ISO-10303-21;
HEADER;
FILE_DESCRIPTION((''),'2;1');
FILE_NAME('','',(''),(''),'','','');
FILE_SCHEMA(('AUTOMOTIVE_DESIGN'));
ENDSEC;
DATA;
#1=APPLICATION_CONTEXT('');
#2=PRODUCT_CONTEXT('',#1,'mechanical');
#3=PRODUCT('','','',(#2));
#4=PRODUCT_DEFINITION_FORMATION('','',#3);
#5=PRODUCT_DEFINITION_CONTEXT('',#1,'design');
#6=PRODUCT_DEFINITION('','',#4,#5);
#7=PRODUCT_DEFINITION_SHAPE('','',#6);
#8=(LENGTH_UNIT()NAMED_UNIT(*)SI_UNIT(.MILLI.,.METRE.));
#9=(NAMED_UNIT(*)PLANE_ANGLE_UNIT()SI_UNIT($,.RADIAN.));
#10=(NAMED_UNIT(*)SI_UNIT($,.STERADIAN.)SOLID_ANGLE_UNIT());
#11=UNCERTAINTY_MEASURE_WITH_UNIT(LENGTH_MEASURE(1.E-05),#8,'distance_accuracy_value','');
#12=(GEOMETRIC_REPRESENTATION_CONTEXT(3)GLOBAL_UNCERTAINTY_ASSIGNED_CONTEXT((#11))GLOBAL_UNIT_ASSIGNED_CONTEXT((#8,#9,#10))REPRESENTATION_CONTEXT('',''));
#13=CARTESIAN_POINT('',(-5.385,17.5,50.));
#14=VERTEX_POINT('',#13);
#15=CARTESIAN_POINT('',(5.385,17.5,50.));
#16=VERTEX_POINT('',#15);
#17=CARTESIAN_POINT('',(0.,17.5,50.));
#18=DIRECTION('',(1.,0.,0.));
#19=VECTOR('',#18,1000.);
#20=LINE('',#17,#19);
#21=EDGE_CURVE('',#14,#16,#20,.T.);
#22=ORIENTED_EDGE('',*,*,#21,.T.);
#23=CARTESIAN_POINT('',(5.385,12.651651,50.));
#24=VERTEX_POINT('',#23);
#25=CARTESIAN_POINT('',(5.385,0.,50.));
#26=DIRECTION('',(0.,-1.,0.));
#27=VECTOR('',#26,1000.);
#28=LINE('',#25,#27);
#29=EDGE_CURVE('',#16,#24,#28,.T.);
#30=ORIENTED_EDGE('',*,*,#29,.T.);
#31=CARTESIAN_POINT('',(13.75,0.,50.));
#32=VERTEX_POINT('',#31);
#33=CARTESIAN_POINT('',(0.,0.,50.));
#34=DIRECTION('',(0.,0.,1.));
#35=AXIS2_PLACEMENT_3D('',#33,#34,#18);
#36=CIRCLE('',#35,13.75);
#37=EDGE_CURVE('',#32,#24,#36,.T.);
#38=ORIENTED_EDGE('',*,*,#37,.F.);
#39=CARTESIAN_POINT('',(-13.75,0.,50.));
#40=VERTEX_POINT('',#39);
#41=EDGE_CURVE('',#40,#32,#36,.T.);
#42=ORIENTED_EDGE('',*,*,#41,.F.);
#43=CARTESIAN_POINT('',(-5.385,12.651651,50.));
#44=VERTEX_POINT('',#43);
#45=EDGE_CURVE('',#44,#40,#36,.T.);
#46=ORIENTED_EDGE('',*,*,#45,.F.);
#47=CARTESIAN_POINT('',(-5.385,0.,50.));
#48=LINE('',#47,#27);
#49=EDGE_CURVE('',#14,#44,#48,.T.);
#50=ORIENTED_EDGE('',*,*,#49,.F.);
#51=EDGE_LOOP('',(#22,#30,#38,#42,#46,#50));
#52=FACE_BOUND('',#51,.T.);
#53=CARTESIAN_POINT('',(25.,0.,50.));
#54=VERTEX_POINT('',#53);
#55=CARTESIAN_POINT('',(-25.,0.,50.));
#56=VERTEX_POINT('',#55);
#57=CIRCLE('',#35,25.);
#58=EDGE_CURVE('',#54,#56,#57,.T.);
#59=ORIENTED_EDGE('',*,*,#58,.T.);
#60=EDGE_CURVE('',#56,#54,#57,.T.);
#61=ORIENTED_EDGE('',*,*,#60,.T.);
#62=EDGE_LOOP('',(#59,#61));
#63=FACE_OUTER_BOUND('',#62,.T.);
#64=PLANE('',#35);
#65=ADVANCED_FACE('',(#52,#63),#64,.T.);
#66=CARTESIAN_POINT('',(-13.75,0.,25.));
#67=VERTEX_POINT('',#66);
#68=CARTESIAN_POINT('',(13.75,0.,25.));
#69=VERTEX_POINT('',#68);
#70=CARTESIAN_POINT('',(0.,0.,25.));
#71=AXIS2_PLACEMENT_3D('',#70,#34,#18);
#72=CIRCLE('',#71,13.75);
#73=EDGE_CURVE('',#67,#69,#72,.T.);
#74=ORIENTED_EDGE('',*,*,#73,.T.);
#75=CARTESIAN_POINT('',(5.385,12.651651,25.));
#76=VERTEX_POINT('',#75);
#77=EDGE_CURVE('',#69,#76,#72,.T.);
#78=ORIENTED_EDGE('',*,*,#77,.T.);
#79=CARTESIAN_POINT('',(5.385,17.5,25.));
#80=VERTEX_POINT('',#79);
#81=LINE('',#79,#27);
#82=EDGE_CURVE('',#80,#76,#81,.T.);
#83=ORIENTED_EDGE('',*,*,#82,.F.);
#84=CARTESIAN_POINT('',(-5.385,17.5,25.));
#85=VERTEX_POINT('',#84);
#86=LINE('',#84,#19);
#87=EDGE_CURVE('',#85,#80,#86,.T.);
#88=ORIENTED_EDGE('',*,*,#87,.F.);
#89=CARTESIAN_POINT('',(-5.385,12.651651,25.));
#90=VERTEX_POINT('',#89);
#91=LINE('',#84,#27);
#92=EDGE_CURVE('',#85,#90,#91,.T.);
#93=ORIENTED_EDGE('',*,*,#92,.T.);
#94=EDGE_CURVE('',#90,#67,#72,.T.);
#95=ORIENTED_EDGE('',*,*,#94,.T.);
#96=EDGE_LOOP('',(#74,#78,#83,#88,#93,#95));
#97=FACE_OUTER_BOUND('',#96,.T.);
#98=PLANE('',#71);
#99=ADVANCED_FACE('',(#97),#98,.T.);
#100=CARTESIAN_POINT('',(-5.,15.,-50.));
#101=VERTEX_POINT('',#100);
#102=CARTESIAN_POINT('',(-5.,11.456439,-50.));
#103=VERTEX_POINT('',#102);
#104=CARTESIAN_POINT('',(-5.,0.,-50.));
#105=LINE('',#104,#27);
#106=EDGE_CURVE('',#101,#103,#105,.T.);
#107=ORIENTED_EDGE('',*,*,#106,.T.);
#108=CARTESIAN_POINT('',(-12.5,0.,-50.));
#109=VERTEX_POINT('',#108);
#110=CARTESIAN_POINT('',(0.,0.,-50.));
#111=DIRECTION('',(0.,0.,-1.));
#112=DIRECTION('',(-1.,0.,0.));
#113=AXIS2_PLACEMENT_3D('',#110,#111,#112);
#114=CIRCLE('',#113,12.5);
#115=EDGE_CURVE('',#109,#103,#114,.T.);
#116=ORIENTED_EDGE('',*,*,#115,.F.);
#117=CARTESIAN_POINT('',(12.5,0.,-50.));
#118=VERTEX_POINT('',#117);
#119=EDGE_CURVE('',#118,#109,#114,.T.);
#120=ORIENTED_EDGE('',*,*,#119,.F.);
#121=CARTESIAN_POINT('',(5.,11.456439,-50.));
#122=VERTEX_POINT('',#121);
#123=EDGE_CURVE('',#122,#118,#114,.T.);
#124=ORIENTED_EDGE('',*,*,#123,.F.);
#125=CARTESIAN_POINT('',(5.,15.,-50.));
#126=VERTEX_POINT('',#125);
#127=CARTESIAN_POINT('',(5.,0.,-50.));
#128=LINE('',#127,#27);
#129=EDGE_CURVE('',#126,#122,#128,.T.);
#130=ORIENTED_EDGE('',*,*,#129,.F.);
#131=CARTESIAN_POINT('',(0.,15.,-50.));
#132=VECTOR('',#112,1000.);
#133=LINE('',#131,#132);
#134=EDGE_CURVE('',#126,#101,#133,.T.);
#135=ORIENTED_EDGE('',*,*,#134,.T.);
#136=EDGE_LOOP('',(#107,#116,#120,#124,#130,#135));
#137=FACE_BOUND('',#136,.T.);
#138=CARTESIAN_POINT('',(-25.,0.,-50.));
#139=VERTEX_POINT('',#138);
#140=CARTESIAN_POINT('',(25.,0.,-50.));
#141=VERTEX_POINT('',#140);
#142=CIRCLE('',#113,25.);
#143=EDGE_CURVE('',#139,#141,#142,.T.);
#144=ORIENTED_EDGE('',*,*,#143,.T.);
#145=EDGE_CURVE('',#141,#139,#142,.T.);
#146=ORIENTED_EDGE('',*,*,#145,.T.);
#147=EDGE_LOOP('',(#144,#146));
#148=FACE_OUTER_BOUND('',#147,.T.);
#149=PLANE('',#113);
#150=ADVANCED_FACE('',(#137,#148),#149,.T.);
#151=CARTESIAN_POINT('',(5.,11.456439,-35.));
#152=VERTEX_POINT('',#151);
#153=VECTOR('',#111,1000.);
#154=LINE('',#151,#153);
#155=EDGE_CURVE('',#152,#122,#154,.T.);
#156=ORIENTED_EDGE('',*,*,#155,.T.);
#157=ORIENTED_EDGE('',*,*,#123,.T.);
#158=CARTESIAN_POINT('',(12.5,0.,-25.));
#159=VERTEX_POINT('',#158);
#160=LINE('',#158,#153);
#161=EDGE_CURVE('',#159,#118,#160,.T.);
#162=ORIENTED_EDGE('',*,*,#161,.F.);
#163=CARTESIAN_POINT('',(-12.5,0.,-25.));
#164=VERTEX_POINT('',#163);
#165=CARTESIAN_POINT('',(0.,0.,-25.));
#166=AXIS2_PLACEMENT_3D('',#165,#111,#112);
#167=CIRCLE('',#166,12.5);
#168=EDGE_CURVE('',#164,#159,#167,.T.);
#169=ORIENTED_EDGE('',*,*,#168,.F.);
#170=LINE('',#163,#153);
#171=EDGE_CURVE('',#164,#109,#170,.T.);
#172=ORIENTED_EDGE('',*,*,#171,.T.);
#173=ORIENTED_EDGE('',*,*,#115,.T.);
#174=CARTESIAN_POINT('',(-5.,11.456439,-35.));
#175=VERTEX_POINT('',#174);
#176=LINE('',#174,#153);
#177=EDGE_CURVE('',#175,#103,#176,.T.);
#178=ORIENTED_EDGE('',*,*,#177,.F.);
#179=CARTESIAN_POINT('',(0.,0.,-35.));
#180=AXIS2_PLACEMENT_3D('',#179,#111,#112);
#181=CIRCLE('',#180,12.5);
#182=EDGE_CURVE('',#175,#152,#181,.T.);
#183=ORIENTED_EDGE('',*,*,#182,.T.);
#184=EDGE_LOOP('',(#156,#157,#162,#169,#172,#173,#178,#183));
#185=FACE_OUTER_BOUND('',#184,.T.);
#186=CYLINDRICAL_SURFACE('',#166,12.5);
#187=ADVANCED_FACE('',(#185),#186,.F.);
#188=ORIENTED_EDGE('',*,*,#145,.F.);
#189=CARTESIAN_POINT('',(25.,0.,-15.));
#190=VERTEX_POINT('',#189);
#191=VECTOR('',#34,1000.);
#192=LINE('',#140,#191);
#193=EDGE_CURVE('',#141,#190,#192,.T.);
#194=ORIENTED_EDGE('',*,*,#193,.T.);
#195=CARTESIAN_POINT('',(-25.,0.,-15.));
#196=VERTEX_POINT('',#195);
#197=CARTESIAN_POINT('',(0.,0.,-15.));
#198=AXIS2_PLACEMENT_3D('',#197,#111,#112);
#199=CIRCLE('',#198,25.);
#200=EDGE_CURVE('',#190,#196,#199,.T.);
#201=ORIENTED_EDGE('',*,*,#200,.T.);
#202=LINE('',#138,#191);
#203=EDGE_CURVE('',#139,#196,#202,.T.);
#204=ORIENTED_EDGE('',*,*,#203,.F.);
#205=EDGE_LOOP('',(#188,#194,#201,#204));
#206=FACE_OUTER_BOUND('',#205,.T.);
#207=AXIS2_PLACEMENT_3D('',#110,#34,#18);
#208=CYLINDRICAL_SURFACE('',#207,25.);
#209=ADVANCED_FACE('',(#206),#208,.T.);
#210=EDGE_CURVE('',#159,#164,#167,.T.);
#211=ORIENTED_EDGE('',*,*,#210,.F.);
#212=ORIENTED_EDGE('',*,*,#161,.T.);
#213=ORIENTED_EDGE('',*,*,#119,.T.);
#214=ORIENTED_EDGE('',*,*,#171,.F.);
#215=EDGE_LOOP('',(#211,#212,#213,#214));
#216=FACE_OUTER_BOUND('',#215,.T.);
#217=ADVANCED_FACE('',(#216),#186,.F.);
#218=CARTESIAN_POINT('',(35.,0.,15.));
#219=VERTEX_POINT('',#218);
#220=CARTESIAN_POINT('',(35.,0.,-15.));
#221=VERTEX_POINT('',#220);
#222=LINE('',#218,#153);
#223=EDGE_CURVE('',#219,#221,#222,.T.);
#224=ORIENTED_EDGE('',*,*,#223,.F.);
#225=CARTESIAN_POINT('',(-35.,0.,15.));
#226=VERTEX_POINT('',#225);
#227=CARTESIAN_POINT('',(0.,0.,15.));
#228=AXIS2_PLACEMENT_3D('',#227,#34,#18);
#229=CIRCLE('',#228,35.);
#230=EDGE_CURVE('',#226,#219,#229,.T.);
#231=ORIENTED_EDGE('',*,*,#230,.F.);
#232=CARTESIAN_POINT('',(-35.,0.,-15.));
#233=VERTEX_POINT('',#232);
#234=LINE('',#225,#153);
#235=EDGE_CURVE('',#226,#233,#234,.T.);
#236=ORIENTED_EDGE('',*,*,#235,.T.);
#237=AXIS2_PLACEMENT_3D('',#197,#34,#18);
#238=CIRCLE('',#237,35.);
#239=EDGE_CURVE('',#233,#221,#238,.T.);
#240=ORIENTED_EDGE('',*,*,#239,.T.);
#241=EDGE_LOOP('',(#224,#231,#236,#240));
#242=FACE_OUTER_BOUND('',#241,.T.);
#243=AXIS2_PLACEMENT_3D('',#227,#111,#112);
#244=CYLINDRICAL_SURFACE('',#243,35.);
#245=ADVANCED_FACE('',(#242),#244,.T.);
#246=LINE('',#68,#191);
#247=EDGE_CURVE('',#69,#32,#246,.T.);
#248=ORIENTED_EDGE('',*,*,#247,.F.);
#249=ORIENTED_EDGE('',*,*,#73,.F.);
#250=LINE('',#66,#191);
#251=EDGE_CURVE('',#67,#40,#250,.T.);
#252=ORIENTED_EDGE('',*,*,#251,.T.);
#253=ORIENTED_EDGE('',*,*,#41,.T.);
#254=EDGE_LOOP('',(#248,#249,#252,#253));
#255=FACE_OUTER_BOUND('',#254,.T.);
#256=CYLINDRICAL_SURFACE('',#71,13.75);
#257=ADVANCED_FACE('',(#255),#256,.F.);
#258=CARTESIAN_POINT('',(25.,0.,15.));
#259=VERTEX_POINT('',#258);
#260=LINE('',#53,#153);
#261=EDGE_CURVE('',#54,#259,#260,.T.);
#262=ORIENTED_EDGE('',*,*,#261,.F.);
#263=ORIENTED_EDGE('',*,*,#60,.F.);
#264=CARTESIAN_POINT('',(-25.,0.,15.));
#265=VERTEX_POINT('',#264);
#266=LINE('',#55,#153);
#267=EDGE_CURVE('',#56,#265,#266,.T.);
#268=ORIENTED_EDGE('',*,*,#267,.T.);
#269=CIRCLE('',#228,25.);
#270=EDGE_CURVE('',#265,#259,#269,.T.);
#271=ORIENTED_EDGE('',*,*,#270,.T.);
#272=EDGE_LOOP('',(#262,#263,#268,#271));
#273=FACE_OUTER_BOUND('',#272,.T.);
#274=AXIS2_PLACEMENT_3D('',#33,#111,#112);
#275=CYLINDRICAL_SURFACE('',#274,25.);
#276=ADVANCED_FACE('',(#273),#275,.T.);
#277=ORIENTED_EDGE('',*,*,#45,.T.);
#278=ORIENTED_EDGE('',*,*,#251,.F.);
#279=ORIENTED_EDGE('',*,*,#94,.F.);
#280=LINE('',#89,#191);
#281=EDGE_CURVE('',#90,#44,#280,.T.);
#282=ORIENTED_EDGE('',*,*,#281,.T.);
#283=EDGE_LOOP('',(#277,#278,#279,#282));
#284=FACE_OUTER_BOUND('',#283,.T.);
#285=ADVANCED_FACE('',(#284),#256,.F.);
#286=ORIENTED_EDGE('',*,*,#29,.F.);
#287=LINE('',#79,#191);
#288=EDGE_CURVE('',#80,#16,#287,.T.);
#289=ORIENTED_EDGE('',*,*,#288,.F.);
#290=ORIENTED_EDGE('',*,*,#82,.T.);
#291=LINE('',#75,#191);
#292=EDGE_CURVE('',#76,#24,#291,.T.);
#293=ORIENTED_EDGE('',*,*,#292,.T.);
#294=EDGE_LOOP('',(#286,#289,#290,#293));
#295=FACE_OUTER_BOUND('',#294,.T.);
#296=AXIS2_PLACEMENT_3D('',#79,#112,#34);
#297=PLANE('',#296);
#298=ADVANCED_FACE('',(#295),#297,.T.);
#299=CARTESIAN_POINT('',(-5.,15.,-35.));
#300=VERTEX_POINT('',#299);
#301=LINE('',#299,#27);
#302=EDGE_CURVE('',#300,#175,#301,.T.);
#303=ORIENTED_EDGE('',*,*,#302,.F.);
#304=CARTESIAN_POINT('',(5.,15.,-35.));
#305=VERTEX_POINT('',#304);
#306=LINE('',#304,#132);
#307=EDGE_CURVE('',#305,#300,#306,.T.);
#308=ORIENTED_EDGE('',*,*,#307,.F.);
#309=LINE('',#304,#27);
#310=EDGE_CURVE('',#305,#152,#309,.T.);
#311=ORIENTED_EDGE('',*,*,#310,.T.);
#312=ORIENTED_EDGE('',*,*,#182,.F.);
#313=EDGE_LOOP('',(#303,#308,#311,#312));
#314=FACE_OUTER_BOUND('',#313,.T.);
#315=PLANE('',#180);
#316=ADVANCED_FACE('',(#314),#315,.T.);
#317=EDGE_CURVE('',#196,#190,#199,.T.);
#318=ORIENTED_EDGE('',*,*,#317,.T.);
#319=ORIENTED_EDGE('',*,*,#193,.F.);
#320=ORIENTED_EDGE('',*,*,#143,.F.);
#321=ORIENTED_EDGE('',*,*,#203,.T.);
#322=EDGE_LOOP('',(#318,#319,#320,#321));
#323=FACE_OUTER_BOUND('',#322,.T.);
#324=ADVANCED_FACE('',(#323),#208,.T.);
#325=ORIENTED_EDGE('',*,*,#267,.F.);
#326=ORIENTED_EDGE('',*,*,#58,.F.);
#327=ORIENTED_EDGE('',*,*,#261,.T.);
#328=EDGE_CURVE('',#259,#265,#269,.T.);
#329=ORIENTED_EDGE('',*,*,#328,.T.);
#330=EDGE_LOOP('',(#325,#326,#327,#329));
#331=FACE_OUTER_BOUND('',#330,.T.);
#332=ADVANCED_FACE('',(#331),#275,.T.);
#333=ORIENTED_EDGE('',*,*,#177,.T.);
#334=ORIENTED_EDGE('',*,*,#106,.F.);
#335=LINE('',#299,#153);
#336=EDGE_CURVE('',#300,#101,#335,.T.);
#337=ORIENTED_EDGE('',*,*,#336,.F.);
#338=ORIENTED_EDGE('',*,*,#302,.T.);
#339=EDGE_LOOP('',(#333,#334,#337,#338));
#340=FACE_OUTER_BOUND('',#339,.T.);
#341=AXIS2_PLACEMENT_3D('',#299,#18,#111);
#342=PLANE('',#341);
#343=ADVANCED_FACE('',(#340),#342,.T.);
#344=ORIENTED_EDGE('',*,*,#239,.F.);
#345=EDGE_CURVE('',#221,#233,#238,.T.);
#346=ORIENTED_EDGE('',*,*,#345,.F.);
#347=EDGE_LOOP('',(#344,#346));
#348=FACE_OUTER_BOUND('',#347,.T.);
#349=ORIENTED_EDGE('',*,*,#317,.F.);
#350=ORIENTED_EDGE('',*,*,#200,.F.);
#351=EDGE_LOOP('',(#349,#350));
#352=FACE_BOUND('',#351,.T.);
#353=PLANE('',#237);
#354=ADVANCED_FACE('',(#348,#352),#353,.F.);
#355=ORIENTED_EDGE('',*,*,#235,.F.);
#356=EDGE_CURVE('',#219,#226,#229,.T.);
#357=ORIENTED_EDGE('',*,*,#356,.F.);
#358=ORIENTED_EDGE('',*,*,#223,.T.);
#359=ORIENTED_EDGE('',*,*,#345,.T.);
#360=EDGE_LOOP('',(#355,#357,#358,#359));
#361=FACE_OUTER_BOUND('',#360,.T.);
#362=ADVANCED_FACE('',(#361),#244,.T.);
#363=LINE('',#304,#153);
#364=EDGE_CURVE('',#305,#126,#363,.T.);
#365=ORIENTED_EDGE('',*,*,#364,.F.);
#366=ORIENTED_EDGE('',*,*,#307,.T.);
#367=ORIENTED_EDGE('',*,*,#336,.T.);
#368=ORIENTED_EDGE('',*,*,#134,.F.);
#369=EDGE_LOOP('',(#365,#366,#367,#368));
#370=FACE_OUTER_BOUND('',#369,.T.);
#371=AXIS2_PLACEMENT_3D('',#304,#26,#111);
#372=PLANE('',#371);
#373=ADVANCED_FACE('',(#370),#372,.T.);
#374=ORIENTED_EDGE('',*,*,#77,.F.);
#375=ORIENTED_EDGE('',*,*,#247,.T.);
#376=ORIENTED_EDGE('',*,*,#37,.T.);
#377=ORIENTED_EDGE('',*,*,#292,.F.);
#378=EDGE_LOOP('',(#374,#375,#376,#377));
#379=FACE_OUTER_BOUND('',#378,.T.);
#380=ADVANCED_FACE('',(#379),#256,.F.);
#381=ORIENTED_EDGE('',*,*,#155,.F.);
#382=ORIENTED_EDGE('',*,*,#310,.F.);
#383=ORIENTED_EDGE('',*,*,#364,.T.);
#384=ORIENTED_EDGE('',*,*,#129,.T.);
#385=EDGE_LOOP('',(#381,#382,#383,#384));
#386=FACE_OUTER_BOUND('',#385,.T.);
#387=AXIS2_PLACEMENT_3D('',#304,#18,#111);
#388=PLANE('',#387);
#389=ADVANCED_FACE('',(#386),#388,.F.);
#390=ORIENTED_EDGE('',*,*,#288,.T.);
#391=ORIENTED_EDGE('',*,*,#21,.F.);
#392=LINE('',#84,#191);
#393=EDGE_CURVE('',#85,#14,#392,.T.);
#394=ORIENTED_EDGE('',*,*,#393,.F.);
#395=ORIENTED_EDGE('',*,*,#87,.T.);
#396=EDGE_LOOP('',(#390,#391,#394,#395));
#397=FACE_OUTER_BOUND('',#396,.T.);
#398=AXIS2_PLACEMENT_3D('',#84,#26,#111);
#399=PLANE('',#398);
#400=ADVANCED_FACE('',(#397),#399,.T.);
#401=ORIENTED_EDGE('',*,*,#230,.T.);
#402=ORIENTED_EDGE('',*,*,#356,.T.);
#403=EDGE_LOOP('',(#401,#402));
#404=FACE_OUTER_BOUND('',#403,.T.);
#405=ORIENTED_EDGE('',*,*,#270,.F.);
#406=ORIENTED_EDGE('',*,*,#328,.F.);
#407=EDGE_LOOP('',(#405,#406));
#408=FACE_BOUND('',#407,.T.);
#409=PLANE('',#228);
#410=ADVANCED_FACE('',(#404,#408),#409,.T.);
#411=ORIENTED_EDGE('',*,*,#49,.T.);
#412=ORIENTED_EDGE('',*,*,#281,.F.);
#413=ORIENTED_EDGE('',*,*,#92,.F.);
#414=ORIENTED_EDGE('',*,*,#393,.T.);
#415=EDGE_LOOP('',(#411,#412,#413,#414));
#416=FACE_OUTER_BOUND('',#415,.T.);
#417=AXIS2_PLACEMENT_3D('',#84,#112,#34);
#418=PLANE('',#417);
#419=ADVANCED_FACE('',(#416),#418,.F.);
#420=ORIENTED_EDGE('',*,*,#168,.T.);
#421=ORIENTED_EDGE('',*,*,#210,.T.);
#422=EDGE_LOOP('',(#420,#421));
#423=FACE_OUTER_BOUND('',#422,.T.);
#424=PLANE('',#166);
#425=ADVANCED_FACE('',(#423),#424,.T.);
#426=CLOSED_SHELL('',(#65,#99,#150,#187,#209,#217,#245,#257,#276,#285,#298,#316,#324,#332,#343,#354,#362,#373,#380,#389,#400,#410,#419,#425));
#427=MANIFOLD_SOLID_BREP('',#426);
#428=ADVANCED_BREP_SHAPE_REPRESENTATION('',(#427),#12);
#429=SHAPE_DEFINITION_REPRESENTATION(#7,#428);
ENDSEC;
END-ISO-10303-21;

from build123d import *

# Parameters (mm, degrees)
SKETCH_1_R          = 35
EXTRUDE_1_DEPTH     = 15
SKETCH_2_R          = 25
EXTRUDE_2_DEPTH     = 35
EXTRUDE_START       = 35
SKETCH_3_R          = 25
EXTRUDE_3_DEPTH     = 35
CUT_EXTRUDE_1_DEPTH = 25
SKETCH_5_R          = 12.5
CUT_EXTRUDE_2_DEPTH = 25
CUT_EXTRUDE_3_DEPTH = 15


with BuildPart() as part:
    # 草图1 → 凸台-拉伸1 (new, symmetric)
    with BuildSketch(Plane.XY):
        Circle(SKETCH_1_R)
    extrude(amount=EXTRUDE_1_DEPTH, both=True)

    # 草图2 → 凸台-拉伸2 (add)
    with BuildSketch(Plane.XY.offset(15)):
        Circle(SKETCH_2_R)
    extrude(amount=EXTRUDE_2_DEPTH)

    # 草图3 → 凸台-拉伸3 (add)
    with BuildSketch(Plane(origin=(0, 0, -15), x_dir=(-1, 0, 0), z_dir=(0, 0, -1)).offset(EXTRUDE_START)):
        with Locations(Location((0, 0, 0), (0, 0, 180))):
            Circle(SKETCH_3_R)
    extrude(amount=-EXTRUDE_3_DEPTH)

    # 草图4 → 切除-拉伸1 (cut, symmetric)
    with BuildSketch(Plane.XY.offset(50)):
        with BuildLine():
            Line((-5.385, 17.5), (5.385, 17.5))
            Line((5.385, 17.5), (5.385, 12.651651078))
            ThreePointArc((5.385, 12.651651078), (0, -13.75), (-5.385, 12.651651078))
            Line((-5.385, 12.651651078), (-5.385, 17.5))
        make_face()
    extrude(amount=CUT_EXTRUDE_1_DEPTH, both=True, mode=Mode.SUBTRACT)

    # 草图5 → 切除-拉伸2 (cut, symmetric)
    with BuildSketch(Plane(origin=(0, 0, -50), x_dir=(-1, 0, 0), z_dir=(0, 0, -1))):
        Circle(SKETCH_5_R)
    extrude(amount=CUT_EXTRUDE_2_DEPTH, both=True, mode=Mode.SUBTRACT)

    # 草图6 → 切除-拉伸3 (cut, symmetric)
    with BuildSketch(Plane(origin=(0, 0, -50), x_dir=(-1, 0, 0), z_dir=(0, 0, -1))):
        with BuildLine():
            Line((-5, 15), (5, 15))
            Line((5, 15), (5, 11.456439237))
            ThreePointArc((5, 11.456439237), (0, 12.5), (-5, 11.456439237))
            Line((-5, 11.456439237), (-5, 15))
        make_face()
    extrude(amount=CUT_EXTRUDE_3_DEPTH, both=True, mode=Mode.SUBTRACT)


solid = part.part
